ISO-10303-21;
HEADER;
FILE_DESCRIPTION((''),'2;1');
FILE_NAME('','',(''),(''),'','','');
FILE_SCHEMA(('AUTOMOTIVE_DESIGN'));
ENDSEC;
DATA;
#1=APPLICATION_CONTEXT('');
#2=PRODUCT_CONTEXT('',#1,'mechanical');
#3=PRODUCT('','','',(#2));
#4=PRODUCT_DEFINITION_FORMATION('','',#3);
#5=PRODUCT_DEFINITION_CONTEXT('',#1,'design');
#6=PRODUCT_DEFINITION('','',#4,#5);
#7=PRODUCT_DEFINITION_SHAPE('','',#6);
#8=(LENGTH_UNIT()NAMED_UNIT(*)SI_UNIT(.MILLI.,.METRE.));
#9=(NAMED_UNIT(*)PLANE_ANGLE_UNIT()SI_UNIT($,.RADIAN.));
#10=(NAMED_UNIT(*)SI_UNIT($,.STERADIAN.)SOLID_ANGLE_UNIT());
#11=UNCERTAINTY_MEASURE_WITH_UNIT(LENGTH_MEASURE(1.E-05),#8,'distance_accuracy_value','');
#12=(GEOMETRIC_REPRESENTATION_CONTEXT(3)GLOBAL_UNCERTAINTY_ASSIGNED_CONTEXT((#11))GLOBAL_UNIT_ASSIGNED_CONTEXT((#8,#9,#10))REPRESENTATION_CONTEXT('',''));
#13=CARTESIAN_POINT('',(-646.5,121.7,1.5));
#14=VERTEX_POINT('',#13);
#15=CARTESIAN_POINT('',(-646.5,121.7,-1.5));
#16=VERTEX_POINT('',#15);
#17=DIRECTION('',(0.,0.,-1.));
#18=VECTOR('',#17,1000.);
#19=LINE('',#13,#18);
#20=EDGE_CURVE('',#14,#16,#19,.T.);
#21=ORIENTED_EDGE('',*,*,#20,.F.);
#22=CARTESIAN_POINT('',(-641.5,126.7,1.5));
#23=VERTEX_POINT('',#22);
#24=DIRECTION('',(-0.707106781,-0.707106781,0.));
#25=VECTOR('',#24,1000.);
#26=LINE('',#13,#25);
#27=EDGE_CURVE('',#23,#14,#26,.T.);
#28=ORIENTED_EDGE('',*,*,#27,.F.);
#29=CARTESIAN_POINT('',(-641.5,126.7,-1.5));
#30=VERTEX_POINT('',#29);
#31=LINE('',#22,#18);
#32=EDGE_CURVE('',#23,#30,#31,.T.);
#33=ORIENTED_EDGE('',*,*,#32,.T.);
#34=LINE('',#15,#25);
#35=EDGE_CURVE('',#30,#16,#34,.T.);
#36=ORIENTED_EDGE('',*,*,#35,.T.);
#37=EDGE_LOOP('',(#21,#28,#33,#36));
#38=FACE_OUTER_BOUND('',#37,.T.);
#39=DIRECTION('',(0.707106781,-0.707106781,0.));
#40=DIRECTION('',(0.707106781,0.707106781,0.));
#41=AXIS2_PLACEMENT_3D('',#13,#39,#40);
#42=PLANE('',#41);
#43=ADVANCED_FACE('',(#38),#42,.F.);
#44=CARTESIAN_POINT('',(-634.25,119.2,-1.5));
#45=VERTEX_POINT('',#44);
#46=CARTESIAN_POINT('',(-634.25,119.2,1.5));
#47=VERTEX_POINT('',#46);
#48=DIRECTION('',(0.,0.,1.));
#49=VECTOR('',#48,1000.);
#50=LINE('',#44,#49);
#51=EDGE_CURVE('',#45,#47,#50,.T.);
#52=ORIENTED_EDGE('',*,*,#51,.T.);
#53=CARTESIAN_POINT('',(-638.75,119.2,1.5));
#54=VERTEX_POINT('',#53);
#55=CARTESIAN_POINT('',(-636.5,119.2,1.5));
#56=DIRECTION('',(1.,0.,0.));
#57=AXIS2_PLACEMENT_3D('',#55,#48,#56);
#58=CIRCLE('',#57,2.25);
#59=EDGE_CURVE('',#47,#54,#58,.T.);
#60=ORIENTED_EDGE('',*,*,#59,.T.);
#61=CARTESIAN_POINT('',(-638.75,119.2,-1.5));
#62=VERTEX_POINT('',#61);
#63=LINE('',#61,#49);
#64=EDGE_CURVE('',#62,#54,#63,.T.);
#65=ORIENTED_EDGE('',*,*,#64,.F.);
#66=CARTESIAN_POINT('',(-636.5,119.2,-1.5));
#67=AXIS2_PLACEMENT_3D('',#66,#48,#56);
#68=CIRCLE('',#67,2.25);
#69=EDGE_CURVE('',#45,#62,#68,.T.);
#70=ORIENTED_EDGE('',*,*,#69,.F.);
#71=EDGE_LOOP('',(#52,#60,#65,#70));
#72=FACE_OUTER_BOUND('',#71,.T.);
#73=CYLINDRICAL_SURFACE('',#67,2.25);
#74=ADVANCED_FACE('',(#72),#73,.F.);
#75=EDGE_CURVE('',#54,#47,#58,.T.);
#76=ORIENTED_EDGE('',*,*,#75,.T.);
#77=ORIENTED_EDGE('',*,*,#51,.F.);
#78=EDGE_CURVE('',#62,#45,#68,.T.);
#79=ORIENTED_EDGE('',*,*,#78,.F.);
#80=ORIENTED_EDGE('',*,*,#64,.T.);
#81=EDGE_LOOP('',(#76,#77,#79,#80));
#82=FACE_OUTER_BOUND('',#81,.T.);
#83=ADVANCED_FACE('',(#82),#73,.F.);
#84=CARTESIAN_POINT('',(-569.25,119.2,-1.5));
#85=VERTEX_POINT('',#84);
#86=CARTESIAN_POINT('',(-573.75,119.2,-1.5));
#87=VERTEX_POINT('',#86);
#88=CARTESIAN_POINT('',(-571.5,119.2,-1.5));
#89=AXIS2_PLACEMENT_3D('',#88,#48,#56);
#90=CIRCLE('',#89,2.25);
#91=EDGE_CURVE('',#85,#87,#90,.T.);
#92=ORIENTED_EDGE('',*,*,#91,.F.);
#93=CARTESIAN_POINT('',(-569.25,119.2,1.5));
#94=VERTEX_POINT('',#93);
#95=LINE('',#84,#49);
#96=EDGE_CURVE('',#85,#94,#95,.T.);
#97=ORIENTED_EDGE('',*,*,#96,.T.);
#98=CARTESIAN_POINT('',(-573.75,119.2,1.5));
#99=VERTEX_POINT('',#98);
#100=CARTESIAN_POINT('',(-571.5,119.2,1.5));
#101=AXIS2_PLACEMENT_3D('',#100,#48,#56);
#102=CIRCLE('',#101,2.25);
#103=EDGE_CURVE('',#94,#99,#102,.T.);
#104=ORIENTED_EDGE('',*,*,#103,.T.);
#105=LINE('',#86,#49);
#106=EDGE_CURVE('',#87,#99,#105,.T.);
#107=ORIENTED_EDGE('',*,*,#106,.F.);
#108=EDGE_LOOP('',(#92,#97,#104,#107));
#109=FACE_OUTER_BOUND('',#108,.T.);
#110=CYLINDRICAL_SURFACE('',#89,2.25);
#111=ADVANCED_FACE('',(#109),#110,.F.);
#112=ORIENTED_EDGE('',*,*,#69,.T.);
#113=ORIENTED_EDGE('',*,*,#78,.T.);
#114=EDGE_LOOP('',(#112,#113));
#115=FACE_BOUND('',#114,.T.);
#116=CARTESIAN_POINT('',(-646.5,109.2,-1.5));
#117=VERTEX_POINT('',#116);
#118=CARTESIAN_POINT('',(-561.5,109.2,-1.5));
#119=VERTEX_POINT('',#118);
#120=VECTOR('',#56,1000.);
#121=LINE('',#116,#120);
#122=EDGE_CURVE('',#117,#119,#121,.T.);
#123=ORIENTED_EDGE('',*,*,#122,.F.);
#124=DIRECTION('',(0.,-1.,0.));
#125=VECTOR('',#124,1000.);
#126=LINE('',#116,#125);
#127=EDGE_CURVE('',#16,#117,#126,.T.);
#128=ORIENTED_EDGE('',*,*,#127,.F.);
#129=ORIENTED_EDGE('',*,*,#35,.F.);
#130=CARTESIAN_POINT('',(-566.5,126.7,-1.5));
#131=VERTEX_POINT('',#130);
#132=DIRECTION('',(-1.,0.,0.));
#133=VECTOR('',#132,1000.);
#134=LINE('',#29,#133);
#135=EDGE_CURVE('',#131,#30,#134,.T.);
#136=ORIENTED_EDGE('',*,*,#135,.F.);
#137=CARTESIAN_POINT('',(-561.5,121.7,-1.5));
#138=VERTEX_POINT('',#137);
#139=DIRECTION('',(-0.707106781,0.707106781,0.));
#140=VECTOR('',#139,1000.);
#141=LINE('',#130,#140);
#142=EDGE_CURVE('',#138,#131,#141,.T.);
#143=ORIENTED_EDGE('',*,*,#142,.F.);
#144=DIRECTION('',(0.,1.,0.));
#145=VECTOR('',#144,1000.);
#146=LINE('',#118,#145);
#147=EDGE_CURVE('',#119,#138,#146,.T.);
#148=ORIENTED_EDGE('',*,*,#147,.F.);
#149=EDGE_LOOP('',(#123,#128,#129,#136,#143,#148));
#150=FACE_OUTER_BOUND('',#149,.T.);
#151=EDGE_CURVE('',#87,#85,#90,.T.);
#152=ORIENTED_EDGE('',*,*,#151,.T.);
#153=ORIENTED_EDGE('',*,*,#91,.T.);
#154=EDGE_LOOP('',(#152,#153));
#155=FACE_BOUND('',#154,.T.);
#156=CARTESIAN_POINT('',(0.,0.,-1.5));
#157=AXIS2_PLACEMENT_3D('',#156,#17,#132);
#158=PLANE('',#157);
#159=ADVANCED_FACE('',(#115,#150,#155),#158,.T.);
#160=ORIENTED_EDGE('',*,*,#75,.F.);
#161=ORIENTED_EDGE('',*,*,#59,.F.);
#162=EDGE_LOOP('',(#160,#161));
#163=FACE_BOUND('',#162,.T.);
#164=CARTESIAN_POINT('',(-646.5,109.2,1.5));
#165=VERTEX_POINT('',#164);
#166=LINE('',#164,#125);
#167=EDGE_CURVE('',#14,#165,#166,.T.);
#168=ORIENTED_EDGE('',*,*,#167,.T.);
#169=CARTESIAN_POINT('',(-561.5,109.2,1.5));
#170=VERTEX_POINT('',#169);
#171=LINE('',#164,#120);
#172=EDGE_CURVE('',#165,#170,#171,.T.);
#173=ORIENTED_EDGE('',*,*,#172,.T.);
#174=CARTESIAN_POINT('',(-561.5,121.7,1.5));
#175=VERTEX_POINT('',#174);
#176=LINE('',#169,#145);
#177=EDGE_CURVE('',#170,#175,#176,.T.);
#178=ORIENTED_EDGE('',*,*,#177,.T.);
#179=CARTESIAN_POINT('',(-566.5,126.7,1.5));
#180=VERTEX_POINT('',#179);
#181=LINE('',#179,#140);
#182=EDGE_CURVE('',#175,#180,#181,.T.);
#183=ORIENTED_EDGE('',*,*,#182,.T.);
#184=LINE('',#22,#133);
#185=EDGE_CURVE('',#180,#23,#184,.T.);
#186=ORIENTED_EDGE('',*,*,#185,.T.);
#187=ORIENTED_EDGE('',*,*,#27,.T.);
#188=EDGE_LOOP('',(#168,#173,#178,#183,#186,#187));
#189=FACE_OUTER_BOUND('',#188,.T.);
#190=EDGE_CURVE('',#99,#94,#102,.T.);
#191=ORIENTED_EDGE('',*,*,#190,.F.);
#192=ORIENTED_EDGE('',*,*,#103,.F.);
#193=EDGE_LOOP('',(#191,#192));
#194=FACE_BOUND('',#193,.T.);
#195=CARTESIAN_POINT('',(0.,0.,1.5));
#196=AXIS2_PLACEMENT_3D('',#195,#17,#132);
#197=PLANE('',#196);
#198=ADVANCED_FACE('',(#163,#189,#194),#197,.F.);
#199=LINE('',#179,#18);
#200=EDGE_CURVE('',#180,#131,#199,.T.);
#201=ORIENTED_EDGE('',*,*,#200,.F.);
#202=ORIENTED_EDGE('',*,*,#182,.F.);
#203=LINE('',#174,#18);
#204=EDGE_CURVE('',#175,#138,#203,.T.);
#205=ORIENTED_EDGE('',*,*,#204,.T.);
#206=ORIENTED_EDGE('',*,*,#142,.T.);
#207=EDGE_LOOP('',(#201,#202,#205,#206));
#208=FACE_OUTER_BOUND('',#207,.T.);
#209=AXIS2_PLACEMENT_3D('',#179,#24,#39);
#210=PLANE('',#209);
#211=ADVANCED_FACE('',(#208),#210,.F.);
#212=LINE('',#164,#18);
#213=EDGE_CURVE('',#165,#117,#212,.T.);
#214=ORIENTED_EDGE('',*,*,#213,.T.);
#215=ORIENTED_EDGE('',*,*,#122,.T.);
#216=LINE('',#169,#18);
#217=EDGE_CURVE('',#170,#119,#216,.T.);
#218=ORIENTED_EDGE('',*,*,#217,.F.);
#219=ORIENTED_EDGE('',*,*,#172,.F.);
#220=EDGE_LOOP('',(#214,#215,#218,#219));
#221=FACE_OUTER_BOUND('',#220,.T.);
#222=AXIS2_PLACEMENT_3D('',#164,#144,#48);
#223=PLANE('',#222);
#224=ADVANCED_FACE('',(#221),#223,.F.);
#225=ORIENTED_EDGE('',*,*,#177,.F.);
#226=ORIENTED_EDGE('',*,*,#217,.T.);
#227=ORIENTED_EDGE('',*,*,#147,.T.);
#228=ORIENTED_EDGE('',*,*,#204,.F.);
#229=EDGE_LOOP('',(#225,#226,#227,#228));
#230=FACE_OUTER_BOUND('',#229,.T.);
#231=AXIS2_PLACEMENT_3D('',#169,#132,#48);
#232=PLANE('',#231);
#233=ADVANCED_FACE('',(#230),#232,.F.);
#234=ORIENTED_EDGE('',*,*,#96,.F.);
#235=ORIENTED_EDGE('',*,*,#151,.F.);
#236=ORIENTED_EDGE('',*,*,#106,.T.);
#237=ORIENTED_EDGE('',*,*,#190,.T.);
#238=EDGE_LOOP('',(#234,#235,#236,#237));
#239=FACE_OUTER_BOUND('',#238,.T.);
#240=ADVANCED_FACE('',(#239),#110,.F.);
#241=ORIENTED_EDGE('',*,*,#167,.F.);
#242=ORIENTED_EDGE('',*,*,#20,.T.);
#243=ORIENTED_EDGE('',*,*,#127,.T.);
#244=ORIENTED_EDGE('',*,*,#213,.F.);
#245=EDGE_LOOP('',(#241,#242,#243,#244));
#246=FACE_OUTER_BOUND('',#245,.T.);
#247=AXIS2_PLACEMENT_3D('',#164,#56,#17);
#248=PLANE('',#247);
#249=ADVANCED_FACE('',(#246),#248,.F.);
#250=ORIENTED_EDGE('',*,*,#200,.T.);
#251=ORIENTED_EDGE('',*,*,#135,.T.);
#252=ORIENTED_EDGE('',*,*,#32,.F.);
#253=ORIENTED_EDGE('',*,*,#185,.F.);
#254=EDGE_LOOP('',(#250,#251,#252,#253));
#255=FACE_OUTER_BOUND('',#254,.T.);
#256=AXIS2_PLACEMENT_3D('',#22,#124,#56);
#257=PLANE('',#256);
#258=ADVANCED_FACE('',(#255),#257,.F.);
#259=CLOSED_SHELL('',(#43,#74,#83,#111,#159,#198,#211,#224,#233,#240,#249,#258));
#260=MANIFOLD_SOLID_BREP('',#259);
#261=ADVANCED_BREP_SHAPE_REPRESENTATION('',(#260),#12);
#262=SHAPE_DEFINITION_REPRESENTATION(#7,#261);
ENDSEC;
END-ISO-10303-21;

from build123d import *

# Parameters (mm, degrees)
BOSS_EXTRUDE1_DEPTH = 1.5
SKETCH2_R           = 2.25
CUT_EXTRUDE1_DEPTH  = 3


with BuildPart() as part:
    # Sketch1 → Boss-Extrude1 (new, symmetric)
    with BuildSketch(Plane.XY):
        Polygon((-646.5, 109.2), (-561.5, 109.2), (-561.5, 121.7), (-566.5, 126.7), (-641.5, 126.7), (-646.5, 121.7), align=None)
    extrude(amount=BOSS_EXTRUDE1_DEPTH, both=True)

    # Sketch2 → Cut-Extrude1 (cut)
    with BuildSketch(Plane.XY.offset(1.5)):
        with Locations((-636.5, 119.2)):
            Circle(SKETCH2_R)
        with Locations((-571.5, 119.2)):
            Circle(SKETCH2_R)
    extrude(amount=-CUT_EXTRUDE1_DEPTH, mode=Mode.SUBTRACT)


solid = part.part
